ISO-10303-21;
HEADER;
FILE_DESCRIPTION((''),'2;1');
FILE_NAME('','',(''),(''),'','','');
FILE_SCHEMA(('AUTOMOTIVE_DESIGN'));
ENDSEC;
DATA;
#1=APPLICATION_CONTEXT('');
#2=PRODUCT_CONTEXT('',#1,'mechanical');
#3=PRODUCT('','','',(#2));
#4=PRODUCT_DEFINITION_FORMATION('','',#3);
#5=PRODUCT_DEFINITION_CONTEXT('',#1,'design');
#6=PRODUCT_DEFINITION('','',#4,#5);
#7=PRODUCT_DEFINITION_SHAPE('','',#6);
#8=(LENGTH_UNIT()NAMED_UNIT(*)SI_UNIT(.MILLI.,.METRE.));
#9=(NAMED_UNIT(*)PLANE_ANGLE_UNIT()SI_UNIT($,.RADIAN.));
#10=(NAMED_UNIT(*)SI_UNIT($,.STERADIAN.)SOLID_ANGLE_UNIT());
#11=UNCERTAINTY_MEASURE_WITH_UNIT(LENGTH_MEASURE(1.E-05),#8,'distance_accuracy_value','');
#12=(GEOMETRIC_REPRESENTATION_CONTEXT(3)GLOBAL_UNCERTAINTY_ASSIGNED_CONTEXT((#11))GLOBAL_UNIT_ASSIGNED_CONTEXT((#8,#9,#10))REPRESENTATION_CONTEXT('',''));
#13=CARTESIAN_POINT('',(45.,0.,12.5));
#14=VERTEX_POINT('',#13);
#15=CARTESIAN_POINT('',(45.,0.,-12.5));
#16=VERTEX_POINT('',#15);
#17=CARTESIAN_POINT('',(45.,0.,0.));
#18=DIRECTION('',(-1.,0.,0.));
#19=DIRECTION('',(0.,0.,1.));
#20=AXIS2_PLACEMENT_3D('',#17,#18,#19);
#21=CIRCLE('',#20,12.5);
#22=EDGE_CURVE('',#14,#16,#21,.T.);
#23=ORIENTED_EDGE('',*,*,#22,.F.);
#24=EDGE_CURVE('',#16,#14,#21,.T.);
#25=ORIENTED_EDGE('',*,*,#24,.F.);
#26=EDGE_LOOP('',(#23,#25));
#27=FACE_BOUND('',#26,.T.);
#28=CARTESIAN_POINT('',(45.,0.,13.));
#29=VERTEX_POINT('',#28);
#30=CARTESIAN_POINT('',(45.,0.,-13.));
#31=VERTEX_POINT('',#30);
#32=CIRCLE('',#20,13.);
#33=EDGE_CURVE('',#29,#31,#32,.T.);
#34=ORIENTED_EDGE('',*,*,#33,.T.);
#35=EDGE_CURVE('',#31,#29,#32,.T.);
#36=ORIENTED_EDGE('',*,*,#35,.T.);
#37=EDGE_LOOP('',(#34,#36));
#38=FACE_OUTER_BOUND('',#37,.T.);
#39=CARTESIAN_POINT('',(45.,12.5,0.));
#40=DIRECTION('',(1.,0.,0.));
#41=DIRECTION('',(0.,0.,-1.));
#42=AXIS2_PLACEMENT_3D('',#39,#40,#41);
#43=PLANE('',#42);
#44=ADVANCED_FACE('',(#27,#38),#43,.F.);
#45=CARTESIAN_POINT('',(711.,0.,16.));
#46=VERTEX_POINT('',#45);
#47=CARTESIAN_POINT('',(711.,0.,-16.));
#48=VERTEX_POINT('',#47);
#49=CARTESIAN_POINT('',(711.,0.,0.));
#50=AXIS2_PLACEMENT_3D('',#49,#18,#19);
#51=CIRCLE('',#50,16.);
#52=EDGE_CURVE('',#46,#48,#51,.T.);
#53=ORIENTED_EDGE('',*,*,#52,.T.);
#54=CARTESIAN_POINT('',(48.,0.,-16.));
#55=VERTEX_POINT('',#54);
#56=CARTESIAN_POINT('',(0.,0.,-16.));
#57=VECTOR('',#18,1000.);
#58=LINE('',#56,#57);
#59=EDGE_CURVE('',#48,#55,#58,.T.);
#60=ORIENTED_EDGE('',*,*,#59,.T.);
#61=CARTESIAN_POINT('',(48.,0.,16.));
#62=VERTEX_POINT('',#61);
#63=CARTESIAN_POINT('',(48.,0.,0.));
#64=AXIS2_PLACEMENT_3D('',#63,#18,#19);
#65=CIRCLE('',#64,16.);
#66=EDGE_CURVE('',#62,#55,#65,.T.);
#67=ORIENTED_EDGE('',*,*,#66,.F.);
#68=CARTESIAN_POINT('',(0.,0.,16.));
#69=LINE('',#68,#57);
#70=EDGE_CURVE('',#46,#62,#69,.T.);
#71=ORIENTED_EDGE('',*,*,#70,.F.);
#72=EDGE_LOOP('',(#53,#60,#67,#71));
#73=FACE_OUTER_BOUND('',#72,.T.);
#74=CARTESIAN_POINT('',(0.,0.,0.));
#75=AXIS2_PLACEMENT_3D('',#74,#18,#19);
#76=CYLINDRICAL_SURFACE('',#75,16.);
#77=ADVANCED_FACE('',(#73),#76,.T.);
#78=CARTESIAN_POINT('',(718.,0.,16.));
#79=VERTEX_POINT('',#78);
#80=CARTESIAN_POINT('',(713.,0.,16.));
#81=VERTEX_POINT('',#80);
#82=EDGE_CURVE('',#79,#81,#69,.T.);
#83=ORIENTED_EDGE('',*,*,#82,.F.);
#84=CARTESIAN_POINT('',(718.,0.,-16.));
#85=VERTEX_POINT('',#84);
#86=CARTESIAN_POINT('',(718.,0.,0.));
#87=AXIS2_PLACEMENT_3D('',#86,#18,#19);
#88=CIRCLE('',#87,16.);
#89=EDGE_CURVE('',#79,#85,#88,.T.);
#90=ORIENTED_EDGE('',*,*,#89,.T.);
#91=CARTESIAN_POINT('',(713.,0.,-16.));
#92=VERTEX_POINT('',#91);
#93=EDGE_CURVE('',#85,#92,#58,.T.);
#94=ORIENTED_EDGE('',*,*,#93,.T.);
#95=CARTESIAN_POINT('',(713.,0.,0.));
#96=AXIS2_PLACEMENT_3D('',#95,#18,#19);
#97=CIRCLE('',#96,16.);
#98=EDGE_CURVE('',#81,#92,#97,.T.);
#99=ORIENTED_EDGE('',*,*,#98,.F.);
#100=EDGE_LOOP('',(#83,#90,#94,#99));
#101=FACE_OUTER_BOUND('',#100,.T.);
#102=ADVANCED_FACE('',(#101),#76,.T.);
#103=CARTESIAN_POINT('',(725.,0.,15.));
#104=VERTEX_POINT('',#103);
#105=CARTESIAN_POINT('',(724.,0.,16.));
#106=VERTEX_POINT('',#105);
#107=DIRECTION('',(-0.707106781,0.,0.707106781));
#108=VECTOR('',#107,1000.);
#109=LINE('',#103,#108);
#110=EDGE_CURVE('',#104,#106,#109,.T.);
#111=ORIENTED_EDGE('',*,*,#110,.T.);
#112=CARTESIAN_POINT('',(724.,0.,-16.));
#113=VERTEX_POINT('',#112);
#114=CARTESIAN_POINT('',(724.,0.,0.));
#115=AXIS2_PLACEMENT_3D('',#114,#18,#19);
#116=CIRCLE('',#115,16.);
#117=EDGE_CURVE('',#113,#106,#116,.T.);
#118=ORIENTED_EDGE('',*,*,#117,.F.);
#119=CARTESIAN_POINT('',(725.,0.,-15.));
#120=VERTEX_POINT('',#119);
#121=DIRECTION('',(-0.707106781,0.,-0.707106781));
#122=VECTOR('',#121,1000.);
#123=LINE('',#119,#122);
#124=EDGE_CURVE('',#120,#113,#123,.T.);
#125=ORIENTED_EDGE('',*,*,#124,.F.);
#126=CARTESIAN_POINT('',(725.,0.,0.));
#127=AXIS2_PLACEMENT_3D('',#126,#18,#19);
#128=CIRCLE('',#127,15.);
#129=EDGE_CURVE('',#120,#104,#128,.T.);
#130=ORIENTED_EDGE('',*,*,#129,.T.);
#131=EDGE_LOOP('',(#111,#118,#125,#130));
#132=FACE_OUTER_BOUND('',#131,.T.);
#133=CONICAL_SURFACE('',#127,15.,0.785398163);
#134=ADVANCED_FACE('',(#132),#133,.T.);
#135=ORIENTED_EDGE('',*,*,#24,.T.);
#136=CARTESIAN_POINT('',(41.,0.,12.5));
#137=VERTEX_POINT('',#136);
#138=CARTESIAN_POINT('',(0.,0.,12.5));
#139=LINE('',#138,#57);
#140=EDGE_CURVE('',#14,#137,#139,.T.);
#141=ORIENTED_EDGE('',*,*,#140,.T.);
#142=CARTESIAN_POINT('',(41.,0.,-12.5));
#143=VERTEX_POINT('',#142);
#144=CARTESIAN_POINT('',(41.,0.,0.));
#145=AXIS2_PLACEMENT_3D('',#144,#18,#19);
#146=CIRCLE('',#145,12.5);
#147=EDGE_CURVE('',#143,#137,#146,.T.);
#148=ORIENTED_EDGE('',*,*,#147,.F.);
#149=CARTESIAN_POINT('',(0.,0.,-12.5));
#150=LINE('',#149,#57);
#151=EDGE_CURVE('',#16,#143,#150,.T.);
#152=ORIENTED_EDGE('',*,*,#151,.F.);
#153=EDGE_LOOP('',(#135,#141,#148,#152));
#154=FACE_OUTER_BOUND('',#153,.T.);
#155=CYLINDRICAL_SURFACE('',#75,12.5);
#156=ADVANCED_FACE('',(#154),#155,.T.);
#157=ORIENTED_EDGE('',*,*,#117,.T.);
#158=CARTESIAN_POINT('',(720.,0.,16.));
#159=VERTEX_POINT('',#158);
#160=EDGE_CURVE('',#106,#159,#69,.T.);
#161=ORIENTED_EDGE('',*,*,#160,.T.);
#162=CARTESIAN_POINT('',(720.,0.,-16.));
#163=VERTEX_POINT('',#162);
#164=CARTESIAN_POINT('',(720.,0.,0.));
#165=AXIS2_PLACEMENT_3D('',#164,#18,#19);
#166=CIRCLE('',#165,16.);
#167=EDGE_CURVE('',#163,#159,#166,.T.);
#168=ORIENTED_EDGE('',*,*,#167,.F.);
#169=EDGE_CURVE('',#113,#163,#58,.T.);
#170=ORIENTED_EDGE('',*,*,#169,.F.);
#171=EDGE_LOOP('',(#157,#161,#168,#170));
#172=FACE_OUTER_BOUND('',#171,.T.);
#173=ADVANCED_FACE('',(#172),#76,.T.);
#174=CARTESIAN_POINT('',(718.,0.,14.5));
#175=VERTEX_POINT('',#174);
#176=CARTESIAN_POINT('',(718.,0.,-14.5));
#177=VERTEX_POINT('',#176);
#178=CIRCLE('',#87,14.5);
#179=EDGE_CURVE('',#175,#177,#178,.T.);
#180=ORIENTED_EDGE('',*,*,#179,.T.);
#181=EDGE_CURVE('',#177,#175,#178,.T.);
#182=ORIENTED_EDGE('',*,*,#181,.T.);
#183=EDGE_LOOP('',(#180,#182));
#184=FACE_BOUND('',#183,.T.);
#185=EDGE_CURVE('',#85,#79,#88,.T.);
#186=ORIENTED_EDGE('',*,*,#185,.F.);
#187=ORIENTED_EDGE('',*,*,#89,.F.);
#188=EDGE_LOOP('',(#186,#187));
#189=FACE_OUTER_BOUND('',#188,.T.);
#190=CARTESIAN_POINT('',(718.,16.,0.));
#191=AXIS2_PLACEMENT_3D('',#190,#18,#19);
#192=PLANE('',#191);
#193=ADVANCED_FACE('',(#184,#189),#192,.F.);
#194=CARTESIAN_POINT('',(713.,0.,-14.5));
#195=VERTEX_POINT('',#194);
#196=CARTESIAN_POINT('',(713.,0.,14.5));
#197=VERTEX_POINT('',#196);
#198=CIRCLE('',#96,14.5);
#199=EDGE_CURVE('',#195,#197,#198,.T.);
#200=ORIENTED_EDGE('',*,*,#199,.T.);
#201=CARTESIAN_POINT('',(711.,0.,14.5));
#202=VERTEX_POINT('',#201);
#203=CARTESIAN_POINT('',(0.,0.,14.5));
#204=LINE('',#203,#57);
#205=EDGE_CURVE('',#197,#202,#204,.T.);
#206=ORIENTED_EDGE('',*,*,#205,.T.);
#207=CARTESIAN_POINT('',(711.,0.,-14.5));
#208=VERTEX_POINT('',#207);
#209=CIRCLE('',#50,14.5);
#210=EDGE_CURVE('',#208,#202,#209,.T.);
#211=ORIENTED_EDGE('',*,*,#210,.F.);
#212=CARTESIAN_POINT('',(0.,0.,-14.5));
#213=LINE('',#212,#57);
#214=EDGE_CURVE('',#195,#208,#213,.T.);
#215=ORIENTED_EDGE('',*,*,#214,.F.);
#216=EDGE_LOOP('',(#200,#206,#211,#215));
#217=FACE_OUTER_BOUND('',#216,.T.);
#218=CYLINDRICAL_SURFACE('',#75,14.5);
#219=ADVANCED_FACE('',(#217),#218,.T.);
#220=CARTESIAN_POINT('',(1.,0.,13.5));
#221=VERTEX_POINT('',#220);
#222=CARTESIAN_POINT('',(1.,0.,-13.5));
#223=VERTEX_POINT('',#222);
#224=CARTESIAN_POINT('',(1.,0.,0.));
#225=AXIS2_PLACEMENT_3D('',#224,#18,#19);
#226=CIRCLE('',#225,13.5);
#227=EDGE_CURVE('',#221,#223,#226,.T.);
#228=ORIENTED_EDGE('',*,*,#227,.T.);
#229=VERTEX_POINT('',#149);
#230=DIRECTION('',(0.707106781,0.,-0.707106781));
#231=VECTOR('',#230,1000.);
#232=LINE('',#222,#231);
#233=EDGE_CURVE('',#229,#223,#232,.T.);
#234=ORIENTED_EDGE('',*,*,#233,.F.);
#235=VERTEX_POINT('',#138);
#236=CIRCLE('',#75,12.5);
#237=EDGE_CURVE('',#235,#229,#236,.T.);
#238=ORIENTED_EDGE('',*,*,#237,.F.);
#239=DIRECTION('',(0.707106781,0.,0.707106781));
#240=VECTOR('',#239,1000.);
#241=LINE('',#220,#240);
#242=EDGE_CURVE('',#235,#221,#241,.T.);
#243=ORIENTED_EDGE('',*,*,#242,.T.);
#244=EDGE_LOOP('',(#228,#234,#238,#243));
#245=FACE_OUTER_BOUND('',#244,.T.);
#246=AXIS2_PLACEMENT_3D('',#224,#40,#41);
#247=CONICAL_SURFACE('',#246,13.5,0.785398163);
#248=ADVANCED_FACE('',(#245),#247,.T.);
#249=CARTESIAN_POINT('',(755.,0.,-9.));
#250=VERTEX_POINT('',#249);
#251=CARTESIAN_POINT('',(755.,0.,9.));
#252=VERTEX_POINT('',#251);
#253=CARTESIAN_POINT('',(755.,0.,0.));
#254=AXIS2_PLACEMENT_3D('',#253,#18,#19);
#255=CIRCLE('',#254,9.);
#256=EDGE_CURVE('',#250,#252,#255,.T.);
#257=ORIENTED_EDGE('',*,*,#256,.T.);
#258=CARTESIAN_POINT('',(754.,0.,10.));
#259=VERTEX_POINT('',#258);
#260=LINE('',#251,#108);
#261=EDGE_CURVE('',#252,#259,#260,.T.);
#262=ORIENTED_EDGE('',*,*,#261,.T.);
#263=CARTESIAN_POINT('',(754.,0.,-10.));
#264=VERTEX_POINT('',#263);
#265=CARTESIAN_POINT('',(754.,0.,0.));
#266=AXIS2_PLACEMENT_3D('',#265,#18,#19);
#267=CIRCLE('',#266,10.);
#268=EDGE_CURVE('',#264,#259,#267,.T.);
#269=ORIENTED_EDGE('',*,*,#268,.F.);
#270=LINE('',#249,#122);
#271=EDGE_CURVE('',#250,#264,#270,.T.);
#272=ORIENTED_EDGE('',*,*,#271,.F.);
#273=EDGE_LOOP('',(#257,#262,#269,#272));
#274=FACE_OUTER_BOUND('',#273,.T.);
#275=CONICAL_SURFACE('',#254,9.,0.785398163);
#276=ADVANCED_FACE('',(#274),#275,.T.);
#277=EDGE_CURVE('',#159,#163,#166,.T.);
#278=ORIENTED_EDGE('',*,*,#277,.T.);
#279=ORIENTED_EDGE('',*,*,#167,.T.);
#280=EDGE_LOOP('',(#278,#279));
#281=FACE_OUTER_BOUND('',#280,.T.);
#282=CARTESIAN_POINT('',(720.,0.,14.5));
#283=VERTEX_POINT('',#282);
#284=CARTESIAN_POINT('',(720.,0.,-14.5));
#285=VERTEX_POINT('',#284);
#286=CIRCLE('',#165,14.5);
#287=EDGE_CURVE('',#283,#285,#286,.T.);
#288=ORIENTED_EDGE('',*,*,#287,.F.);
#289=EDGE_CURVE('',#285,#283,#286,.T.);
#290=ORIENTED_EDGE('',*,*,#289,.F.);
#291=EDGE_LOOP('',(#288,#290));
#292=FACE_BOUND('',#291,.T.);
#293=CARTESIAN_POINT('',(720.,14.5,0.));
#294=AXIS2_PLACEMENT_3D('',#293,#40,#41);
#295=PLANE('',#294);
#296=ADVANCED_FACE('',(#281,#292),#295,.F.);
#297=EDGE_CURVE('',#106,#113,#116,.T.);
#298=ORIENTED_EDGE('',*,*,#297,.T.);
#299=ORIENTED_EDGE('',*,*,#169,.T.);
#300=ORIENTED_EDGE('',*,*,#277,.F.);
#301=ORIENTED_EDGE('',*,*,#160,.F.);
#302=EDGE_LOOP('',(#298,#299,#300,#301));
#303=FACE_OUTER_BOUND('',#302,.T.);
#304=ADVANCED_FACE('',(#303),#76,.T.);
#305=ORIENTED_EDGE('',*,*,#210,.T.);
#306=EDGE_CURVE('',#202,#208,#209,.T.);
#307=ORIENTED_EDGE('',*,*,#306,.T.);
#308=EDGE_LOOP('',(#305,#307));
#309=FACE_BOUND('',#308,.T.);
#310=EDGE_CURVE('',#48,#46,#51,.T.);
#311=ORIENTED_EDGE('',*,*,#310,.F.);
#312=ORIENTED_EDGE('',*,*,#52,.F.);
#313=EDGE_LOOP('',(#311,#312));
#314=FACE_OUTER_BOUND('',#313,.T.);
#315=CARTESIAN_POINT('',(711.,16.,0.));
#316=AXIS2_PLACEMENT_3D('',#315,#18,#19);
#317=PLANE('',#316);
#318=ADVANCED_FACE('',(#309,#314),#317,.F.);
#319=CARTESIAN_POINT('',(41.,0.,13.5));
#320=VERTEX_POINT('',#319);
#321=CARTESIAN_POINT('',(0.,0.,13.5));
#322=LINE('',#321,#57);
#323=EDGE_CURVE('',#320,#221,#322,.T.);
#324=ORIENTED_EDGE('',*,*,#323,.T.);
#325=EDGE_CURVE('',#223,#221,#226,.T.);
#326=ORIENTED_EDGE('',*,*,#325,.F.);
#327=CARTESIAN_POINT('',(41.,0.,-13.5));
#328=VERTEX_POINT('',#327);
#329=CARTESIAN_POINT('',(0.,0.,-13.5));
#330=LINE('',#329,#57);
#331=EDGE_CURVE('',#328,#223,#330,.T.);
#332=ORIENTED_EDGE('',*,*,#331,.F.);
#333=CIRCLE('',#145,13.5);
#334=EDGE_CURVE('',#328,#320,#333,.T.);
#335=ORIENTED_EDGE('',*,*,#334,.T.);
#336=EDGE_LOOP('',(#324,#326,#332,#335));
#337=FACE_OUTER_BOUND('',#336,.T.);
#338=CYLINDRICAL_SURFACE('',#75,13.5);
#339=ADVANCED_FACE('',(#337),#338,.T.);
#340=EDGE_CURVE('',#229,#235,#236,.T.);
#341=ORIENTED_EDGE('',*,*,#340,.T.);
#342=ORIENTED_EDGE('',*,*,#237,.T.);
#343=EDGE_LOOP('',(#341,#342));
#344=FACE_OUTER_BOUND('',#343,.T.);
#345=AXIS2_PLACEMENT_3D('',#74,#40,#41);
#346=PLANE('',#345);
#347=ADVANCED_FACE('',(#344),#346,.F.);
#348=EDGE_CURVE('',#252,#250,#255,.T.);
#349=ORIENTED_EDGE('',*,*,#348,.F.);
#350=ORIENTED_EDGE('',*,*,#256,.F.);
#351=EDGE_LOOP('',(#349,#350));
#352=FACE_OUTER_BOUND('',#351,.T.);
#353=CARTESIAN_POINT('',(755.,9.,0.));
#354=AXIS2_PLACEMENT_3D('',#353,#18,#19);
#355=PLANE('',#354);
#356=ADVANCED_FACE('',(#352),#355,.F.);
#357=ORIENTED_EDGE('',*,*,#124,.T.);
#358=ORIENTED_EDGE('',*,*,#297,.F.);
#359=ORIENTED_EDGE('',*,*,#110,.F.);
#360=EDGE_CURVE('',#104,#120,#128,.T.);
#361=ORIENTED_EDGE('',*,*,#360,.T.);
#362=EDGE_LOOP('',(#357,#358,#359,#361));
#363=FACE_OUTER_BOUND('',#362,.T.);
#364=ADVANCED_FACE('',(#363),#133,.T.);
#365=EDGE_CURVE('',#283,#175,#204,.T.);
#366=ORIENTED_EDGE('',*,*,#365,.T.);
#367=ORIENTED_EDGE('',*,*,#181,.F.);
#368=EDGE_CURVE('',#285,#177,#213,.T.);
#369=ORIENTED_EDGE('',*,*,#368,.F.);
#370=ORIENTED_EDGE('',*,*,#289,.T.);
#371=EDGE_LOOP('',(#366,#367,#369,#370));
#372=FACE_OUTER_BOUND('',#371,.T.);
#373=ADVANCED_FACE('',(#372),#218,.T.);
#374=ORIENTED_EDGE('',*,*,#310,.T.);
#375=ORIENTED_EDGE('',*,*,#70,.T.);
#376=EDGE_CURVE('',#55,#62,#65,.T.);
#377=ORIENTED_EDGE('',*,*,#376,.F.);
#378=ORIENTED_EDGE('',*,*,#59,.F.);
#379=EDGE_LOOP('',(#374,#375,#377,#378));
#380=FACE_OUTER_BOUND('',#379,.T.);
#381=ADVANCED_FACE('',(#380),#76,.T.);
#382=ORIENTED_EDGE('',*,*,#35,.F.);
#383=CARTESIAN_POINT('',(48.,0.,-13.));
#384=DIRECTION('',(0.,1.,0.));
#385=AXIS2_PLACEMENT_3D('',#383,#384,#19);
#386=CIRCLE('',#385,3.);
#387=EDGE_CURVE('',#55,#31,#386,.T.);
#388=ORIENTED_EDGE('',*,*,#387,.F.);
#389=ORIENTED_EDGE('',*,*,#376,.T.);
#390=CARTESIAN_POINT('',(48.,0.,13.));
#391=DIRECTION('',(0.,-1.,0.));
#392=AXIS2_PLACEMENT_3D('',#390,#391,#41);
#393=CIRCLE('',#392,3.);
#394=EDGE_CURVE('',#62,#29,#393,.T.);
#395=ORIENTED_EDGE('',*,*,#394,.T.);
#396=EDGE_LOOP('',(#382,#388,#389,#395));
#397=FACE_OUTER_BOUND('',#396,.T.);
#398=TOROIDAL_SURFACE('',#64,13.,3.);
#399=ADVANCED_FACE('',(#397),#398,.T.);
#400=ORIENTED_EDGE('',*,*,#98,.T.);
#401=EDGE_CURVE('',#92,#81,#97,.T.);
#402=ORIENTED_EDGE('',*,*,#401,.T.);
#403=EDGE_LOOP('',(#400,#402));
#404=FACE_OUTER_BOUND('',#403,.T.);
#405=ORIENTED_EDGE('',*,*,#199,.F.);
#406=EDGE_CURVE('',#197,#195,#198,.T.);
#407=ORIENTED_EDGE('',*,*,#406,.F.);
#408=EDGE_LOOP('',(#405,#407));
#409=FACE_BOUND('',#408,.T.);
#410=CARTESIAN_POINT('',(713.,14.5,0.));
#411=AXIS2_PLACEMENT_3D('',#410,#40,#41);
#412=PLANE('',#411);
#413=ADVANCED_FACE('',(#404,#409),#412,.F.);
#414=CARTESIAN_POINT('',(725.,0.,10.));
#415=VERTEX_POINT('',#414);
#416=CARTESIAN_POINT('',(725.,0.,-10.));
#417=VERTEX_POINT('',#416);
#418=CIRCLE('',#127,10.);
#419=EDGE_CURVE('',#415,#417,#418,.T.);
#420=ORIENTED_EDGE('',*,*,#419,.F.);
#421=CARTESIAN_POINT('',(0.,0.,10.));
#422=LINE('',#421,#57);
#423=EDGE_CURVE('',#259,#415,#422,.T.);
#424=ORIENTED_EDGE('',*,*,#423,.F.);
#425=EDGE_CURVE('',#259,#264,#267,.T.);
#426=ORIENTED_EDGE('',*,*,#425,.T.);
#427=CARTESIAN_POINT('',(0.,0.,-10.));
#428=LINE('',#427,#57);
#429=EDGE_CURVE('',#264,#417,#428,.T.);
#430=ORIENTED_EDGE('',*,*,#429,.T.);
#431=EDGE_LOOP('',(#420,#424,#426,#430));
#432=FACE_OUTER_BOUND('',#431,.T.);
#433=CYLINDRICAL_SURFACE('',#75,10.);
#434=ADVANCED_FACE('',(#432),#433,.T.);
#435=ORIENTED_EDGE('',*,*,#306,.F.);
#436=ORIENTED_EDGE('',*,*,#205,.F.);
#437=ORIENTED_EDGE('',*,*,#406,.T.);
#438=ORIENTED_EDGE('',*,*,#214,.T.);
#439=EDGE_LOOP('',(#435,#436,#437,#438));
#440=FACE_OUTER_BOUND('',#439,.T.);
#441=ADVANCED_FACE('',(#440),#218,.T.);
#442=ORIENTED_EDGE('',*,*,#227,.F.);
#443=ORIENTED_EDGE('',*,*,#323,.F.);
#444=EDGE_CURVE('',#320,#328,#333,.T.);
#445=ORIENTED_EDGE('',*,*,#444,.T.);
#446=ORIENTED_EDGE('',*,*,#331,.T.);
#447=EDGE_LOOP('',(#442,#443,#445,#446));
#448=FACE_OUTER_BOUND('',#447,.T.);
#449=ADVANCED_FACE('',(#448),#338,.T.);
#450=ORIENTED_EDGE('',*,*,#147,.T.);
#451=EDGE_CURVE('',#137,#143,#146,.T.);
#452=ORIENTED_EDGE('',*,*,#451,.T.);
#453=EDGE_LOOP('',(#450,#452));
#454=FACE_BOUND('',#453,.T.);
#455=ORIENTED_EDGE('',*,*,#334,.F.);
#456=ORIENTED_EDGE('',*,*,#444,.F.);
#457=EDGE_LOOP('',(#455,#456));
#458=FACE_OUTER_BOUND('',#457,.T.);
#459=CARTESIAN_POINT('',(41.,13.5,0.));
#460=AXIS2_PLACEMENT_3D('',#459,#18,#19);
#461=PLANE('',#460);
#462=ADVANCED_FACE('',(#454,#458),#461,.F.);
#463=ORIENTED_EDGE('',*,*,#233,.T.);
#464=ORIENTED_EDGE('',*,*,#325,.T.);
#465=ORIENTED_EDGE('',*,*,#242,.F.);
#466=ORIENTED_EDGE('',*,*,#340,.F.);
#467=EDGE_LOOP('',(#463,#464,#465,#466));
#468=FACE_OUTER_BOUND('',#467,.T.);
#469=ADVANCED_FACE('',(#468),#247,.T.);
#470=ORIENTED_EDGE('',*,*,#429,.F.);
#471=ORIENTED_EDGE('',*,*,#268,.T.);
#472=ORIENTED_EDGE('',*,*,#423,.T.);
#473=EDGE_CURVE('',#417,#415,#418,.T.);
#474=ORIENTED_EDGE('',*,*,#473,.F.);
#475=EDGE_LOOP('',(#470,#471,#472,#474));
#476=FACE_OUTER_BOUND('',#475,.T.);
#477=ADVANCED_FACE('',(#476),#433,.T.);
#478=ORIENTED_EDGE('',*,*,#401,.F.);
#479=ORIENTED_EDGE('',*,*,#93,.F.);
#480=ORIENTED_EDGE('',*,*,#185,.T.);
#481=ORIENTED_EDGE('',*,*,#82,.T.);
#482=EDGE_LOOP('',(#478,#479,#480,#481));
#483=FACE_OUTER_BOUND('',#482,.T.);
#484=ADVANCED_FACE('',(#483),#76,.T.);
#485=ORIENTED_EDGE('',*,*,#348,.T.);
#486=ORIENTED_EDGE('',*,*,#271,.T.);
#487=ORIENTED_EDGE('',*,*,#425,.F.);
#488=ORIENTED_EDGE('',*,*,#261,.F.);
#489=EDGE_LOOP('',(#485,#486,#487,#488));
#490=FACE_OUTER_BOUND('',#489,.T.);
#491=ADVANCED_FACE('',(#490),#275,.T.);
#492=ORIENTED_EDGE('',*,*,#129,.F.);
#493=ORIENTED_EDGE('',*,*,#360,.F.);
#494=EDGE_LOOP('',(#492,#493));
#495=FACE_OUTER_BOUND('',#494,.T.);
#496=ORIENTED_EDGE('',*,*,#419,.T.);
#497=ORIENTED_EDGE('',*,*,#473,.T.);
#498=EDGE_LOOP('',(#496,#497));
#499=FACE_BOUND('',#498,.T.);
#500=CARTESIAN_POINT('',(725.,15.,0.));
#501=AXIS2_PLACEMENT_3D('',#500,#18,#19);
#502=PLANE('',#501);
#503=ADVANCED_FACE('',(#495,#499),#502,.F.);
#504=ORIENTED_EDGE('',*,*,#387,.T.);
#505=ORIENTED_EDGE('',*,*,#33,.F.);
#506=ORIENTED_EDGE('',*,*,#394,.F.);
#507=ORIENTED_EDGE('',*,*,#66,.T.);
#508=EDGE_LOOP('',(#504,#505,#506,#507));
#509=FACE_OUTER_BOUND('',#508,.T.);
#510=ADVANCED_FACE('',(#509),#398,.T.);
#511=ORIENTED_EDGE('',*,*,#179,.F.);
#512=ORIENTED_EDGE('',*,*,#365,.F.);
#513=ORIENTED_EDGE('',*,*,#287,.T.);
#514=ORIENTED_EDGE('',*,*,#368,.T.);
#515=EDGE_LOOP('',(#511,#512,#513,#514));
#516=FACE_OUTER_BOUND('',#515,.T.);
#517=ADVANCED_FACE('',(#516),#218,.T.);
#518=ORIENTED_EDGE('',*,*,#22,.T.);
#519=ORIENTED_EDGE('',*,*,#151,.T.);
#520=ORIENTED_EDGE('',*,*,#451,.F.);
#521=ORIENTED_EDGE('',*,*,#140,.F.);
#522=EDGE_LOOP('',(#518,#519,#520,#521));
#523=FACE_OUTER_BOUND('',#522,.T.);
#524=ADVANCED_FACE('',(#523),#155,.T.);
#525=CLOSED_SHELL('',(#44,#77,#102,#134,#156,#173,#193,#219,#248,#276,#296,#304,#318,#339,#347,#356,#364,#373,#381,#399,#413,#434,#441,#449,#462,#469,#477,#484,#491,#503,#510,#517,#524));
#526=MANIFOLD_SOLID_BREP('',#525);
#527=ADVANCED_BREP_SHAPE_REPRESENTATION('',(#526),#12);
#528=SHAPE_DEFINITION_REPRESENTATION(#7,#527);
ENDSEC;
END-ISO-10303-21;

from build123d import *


with BuildPart() as part:
    # 草图1 → 旋转1 (revolve)
    with BuildSketch(Plane.XY, mode=Mode.PRIVATE) as revolve_1_sk:
        with BuildLine():
            Line((0, 0), (0, 12.5))
            Line((0, 12.5), (1, 13.5))
            Line((1, 13.5), (41, 13.5))
            Line((41, 13.5), (41, 12.5))
            Line((41, 12.5), (45, 12.5))
            Line((45, 12.5), (45, 13))
            ThreePointArc((45, 13), (45.878679656, 15.121320344), (48, 16))
            Line((48, 16), (711, 16))
            Line((711, 16), (711, 14.5))
            Line((711, 14.5), (713, 14.5))
            Line((713, 14.5), (713, 16))
            Line((713, 16), (718, 16))
            Line((718, 16), (718, 14.5))
            Line((718, 14.5), (720, 14.5))
            Line((720, 14.5), (720, 16))
            Line((720, 16), (724, 16))
            Line((724, 16), (725, 15))
            Line((725, 15), (725, 10))
            Line((725, 10), (754, 10))
            Line((754, 10), (755, 9))
            Line((755, 9), (755, 0))
            Line((755, 0), (0, 0))
        make_face()
    revolve(revolve_1_sk.sketch.rotate(Axis((0, 0, 0), (1, 0, 0)), 90), axis=Axis((0, 0, 0), (1, 0, 0)))


solid = part.part
